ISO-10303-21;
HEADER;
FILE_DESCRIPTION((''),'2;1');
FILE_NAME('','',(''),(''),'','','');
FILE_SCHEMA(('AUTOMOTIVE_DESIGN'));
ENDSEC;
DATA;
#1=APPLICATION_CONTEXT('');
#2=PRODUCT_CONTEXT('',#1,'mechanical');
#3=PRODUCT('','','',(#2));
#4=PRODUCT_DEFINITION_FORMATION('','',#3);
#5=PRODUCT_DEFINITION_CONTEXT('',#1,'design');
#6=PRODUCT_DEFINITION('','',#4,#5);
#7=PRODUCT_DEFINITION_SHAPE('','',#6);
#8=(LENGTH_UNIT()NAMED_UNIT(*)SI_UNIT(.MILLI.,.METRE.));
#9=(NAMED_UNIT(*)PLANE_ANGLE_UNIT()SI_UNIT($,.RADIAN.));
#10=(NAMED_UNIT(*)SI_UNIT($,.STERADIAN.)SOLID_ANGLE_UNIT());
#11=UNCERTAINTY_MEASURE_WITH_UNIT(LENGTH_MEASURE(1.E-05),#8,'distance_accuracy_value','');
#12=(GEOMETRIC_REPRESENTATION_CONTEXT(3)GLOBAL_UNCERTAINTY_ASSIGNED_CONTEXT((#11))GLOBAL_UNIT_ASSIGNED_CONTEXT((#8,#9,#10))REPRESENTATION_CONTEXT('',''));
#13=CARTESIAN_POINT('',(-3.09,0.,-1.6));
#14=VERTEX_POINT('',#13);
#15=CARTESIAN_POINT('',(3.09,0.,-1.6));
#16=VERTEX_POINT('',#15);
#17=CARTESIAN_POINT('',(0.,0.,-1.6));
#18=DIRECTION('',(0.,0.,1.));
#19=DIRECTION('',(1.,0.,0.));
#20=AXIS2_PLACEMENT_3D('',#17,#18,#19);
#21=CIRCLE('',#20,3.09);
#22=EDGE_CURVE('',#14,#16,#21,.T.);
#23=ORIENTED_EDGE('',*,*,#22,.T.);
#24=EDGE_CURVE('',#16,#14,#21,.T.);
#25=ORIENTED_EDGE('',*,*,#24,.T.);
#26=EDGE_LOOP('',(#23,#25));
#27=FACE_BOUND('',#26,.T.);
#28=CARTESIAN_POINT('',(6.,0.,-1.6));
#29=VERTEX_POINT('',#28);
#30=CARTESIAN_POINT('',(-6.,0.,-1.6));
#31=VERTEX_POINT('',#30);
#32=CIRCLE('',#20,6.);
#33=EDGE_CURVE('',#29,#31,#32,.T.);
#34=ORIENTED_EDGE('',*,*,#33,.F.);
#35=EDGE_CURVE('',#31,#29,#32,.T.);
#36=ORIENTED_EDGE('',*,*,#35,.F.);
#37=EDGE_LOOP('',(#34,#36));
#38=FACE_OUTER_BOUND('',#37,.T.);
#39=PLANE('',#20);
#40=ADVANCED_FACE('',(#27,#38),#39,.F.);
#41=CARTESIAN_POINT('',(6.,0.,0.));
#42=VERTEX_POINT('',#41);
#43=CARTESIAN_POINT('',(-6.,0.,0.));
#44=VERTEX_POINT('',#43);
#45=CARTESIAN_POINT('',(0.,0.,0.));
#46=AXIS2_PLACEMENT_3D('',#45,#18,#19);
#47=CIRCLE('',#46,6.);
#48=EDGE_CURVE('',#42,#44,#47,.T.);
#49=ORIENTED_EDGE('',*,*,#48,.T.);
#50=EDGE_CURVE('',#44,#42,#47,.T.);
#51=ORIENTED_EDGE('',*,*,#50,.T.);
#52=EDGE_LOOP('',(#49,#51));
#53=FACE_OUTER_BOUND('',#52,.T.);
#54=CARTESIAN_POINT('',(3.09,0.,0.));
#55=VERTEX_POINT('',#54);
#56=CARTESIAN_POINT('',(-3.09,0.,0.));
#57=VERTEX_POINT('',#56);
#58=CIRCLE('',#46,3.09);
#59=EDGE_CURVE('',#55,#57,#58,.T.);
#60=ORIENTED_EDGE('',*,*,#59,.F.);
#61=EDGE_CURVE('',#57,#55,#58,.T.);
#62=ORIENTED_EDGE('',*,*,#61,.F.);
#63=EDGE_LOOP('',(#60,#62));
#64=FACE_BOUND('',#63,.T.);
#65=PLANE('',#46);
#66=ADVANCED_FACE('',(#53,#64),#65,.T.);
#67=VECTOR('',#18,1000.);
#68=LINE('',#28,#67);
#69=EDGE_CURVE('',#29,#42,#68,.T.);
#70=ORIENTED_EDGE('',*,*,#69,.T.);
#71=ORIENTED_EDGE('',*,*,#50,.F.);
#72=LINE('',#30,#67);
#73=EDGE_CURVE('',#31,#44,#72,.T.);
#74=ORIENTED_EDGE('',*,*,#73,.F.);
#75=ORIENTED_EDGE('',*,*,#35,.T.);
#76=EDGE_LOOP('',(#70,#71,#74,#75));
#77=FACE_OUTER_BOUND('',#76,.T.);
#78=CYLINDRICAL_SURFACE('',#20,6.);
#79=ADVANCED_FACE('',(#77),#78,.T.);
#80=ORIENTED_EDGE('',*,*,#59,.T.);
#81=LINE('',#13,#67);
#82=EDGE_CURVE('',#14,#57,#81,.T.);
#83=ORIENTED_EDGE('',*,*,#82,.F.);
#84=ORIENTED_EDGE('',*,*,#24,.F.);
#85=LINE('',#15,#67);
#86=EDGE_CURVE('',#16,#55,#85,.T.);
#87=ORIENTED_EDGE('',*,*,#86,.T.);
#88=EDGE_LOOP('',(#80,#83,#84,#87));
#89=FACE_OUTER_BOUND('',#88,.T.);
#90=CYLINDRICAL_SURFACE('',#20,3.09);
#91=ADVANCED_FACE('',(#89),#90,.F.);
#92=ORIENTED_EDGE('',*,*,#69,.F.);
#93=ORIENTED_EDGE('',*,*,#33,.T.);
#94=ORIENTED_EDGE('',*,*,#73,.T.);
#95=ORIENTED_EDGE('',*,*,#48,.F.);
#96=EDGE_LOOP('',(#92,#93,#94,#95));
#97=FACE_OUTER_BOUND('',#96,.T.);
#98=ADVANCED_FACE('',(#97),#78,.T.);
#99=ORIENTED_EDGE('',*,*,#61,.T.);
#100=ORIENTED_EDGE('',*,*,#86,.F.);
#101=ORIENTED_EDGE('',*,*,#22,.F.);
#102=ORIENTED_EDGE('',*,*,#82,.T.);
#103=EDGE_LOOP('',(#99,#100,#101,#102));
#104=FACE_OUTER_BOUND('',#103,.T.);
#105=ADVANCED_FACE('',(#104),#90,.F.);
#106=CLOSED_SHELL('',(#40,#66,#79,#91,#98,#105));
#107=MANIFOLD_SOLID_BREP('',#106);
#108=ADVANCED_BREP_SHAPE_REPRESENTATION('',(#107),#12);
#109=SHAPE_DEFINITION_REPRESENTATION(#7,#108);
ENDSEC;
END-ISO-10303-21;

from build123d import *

# Parameters (mm, degrees)
SKETCH1_R          = 6
SKETCH1_R_2        = 3.09
BASE_EXTRUDE_DEPTH = 1.6


with BuildPart() as part:
    # Sketch1 → Base-Extrude (new body)
    with BuildSketch(Plane.XY):
        Circle(SKETCH1_R)
        Circle(SKETCH1_R_2, mode=Mode.SUBTRACT)
    extrude(amount=-BASE_EXTRUDE_DEPTH)


solid = part.part
